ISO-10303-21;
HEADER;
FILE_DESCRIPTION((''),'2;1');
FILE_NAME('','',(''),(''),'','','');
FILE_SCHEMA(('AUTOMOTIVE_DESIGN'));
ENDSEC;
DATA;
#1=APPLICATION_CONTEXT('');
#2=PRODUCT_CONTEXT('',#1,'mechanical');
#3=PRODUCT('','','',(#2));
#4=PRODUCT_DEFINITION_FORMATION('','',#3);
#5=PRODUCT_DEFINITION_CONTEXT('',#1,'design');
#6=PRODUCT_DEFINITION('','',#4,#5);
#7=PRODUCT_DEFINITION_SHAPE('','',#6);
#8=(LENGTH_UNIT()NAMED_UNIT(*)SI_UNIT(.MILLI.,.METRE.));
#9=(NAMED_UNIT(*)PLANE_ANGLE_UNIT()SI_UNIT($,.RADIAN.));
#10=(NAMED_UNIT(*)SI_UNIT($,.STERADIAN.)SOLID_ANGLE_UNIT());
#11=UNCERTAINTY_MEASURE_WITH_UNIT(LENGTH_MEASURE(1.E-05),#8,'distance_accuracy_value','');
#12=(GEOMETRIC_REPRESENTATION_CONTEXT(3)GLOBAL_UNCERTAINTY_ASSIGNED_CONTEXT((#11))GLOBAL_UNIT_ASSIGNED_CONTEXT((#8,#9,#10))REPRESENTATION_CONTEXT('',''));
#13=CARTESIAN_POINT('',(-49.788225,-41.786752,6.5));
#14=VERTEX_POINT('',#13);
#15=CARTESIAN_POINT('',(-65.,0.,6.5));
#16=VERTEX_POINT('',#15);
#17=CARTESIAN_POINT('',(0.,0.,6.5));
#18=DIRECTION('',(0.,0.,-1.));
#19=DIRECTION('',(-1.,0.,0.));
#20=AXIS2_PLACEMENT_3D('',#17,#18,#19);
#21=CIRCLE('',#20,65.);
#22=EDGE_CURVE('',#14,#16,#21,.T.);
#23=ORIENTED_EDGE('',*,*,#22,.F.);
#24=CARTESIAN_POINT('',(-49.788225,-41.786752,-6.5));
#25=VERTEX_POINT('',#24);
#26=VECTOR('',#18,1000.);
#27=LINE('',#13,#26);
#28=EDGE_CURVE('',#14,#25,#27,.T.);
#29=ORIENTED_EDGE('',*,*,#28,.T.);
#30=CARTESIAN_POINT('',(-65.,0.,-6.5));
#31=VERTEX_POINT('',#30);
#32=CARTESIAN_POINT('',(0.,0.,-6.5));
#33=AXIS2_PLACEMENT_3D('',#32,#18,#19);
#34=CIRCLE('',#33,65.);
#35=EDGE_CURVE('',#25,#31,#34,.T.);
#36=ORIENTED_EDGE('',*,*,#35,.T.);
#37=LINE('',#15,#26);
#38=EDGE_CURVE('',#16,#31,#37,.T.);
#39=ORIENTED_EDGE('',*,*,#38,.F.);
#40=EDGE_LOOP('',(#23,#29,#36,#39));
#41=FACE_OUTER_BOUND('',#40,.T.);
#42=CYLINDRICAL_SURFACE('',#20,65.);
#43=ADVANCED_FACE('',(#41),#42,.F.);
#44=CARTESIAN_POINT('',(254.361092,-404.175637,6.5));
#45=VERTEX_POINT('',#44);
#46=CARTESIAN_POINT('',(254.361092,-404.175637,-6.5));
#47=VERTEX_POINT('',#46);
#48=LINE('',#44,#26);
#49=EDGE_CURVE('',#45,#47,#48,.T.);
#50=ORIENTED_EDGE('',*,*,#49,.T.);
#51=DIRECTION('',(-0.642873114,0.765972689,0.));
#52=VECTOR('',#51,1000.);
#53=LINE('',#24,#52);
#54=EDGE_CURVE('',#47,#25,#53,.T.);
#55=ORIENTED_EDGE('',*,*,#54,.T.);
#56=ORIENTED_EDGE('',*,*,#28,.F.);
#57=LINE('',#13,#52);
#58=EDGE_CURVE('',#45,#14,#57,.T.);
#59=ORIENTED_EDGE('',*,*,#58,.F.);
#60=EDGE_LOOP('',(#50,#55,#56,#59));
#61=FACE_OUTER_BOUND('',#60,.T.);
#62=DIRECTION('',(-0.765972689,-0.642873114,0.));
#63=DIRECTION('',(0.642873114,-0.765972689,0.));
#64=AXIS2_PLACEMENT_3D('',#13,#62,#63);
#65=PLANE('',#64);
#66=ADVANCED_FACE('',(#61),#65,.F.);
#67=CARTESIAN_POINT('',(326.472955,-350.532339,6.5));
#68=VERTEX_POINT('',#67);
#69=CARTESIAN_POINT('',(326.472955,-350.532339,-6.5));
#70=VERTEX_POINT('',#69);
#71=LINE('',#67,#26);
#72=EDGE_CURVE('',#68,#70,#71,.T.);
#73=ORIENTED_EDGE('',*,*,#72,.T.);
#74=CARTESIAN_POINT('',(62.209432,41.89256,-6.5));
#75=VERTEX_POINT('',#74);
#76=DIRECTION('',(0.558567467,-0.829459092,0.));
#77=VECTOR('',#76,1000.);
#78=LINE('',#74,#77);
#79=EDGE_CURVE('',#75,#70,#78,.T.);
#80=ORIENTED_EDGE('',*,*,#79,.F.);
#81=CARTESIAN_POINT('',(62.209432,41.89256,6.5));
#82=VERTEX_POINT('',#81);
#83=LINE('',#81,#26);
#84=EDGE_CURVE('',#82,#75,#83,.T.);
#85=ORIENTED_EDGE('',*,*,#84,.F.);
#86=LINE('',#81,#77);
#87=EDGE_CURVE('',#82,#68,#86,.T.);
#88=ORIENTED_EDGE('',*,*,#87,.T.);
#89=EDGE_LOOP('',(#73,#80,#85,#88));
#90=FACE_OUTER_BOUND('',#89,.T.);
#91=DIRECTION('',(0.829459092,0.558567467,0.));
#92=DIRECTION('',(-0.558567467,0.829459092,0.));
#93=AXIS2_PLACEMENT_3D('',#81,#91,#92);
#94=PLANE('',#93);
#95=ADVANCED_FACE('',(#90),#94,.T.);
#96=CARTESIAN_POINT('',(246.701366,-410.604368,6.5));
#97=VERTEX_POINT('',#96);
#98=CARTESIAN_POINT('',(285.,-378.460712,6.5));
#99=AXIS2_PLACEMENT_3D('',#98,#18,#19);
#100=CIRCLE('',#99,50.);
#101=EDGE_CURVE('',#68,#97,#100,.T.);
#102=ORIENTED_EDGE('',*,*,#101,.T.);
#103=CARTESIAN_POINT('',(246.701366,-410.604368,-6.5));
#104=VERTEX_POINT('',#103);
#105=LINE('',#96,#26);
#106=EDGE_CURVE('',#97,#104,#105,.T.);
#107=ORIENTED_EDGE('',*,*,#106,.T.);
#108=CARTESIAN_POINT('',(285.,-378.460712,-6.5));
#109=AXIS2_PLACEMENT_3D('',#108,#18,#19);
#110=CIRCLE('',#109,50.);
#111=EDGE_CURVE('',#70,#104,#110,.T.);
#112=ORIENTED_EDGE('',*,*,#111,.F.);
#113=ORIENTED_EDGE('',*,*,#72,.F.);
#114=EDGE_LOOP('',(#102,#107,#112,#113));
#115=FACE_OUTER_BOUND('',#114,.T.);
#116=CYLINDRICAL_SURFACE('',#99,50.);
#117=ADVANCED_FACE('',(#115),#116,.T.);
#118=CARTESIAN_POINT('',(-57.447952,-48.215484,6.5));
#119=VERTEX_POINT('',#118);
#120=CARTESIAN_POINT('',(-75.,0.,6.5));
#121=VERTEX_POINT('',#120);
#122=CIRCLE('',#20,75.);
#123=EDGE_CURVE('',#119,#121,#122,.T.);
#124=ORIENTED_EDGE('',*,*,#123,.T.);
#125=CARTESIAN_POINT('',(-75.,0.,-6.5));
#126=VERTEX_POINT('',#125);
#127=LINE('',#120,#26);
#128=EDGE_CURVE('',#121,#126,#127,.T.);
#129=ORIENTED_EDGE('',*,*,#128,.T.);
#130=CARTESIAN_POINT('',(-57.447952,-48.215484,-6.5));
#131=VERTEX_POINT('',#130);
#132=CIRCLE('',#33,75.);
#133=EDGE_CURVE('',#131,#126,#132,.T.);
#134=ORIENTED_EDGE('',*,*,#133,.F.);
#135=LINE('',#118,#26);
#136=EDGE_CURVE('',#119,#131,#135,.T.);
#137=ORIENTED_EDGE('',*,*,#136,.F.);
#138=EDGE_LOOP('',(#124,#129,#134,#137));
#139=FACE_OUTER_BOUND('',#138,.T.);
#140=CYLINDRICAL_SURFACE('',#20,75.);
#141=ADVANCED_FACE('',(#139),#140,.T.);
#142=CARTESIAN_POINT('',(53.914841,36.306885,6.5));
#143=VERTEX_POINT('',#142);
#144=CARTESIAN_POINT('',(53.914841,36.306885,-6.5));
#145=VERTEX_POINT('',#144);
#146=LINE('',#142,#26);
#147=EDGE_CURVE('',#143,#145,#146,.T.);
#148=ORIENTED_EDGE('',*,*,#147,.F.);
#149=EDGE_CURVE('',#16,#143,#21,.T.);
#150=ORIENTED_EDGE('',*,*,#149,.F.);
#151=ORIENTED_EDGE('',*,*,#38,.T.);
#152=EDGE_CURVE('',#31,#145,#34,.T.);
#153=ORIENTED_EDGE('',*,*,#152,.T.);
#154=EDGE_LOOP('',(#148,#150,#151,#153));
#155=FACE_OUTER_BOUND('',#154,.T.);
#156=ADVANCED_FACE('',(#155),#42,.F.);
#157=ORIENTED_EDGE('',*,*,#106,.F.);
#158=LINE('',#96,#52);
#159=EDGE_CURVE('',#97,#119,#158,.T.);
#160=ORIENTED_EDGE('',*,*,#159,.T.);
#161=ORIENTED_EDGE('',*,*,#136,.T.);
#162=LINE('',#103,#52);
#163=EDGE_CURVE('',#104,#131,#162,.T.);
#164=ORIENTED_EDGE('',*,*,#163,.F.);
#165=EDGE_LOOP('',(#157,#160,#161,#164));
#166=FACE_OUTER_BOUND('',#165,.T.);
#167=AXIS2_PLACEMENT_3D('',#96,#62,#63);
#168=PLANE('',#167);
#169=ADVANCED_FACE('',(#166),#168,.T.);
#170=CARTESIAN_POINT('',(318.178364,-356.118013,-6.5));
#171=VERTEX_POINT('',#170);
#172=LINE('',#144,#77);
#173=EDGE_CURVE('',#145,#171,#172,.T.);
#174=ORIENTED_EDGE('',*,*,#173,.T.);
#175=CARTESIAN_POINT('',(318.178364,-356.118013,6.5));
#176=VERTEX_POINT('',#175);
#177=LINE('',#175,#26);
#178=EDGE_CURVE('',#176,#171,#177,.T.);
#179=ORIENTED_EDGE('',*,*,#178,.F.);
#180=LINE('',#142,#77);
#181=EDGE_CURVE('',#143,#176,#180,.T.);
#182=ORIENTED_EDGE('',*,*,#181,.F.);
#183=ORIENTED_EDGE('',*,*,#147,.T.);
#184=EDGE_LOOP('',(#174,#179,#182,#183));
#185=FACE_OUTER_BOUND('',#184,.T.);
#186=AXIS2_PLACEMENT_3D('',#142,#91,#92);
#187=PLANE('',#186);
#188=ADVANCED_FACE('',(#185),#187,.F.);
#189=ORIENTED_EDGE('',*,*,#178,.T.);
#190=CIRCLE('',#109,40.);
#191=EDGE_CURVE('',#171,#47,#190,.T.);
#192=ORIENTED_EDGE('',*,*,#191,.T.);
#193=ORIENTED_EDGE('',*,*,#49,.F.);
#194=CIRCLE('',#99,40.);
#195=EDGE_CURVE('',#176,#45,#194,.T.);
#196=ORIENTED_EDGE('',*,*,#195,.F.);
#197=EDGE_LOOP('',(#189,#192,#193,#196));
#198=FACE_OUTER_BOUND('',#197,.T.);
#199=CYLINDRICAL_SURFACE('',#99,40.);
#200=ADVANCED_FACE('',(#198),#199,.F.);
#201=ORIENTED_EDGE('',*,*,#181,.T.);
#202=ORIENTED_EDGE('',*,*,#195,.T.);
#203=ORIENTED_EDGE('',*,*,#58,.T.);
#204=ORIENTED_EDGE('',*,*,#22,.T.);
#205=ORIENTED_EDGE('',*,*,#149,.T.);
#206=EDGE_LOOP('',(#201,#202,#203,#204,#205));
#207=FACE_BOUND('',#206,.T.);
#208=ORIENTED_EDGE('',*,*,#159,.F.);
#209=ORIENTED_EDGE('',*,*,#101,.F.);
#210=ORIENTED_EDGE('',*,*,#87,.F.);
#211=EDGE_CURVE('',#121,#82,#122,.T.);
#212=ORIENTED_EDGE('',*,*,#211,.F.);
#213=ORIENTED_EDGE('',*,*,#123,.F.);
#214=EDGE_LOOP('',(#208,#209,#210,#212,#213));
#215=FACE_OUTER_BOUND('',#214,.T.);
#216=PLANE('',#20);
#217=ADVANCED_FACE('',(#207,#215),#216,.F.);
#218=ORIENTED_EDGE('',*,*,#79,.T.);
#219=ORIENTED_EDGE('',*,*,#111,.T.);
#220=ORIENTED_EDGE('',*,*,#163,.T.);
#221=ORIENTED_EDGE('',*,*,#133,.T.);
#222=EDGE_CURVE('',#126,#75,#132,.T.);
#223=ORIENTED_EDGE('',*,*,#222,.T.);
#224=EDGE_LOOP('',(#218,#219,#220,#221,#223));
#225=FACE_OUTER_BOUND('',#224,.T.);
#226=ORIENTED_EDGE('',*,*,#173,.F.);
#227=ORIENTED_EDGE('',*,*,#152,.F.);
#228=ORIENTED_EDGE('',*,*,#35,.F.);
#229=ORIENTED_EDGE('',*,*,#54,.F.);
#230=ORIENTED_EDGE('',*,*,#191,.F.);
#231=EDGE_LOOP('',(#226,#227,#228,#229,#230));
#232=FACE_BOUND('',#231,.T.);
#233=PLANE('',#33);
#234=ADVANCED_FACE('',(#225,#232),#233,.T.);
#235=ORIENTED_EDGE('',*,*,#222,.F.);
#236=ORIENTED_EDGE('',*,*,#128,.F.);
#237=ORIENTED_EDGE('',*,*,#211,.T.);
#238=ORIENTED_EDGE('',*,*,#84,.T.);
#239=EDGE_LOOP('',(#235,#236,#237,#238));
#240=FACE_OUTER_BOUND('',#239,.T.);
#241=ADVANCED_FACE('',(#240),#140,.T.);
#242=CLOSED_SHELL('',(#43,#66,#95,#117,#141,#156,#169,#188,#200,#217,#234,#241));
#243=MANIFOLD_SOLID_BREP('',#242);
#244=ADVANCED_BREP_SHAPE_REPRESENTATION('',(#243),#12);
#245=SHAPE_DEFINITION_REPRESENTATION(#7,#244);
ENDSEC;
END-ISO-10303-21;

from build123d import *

# Parameters (mm, degrees)
EXTRUDE_THIN1_DEPTH = 6.5


with BuildPart() as part:
    # Sketch2 → Extrude-Thin1 (new, symmetric)
    with BuildSketch(Plane.XY):
        with BuildLine():
            Line((246.701365565, -410.604367651), (-57.447951652, -48.215483519))
            ThreePointArc((-57.447951652, -48.215483519), (-45.116879333, 59.912162365), (62.209431887, 41.892560011))
            Line((62.209431887, 41.892560011), (326.472954592, -350.532338631))
            ThreePointArc((326.472954592, -350.532338631), (315.077919555, -418.402153548), (246.701365565, -410.604367651))
        make_face()
        with BuildLine():
            Line((254.361092452, -404.175636515), (-49.788224765, -41.786752383))
            ThreePointArc((-49.788224765, -41.786752383), (-39.101295422, 51.92387405), (53.914840969, 36.306885343))
            Line((53.914840969, 36.306885343), (318.178363673, -356.118013299))
            ThreePointArc((318.178363673, -356.118013299), (309.062335644, -410.413865233), (254.361092452, -404.175636515))
        make_face(mode=Mode.SUBTRACT)
    extrude(amount=EXTRUDE_THIN1_DEPTH, both=True)


solid = part.part
